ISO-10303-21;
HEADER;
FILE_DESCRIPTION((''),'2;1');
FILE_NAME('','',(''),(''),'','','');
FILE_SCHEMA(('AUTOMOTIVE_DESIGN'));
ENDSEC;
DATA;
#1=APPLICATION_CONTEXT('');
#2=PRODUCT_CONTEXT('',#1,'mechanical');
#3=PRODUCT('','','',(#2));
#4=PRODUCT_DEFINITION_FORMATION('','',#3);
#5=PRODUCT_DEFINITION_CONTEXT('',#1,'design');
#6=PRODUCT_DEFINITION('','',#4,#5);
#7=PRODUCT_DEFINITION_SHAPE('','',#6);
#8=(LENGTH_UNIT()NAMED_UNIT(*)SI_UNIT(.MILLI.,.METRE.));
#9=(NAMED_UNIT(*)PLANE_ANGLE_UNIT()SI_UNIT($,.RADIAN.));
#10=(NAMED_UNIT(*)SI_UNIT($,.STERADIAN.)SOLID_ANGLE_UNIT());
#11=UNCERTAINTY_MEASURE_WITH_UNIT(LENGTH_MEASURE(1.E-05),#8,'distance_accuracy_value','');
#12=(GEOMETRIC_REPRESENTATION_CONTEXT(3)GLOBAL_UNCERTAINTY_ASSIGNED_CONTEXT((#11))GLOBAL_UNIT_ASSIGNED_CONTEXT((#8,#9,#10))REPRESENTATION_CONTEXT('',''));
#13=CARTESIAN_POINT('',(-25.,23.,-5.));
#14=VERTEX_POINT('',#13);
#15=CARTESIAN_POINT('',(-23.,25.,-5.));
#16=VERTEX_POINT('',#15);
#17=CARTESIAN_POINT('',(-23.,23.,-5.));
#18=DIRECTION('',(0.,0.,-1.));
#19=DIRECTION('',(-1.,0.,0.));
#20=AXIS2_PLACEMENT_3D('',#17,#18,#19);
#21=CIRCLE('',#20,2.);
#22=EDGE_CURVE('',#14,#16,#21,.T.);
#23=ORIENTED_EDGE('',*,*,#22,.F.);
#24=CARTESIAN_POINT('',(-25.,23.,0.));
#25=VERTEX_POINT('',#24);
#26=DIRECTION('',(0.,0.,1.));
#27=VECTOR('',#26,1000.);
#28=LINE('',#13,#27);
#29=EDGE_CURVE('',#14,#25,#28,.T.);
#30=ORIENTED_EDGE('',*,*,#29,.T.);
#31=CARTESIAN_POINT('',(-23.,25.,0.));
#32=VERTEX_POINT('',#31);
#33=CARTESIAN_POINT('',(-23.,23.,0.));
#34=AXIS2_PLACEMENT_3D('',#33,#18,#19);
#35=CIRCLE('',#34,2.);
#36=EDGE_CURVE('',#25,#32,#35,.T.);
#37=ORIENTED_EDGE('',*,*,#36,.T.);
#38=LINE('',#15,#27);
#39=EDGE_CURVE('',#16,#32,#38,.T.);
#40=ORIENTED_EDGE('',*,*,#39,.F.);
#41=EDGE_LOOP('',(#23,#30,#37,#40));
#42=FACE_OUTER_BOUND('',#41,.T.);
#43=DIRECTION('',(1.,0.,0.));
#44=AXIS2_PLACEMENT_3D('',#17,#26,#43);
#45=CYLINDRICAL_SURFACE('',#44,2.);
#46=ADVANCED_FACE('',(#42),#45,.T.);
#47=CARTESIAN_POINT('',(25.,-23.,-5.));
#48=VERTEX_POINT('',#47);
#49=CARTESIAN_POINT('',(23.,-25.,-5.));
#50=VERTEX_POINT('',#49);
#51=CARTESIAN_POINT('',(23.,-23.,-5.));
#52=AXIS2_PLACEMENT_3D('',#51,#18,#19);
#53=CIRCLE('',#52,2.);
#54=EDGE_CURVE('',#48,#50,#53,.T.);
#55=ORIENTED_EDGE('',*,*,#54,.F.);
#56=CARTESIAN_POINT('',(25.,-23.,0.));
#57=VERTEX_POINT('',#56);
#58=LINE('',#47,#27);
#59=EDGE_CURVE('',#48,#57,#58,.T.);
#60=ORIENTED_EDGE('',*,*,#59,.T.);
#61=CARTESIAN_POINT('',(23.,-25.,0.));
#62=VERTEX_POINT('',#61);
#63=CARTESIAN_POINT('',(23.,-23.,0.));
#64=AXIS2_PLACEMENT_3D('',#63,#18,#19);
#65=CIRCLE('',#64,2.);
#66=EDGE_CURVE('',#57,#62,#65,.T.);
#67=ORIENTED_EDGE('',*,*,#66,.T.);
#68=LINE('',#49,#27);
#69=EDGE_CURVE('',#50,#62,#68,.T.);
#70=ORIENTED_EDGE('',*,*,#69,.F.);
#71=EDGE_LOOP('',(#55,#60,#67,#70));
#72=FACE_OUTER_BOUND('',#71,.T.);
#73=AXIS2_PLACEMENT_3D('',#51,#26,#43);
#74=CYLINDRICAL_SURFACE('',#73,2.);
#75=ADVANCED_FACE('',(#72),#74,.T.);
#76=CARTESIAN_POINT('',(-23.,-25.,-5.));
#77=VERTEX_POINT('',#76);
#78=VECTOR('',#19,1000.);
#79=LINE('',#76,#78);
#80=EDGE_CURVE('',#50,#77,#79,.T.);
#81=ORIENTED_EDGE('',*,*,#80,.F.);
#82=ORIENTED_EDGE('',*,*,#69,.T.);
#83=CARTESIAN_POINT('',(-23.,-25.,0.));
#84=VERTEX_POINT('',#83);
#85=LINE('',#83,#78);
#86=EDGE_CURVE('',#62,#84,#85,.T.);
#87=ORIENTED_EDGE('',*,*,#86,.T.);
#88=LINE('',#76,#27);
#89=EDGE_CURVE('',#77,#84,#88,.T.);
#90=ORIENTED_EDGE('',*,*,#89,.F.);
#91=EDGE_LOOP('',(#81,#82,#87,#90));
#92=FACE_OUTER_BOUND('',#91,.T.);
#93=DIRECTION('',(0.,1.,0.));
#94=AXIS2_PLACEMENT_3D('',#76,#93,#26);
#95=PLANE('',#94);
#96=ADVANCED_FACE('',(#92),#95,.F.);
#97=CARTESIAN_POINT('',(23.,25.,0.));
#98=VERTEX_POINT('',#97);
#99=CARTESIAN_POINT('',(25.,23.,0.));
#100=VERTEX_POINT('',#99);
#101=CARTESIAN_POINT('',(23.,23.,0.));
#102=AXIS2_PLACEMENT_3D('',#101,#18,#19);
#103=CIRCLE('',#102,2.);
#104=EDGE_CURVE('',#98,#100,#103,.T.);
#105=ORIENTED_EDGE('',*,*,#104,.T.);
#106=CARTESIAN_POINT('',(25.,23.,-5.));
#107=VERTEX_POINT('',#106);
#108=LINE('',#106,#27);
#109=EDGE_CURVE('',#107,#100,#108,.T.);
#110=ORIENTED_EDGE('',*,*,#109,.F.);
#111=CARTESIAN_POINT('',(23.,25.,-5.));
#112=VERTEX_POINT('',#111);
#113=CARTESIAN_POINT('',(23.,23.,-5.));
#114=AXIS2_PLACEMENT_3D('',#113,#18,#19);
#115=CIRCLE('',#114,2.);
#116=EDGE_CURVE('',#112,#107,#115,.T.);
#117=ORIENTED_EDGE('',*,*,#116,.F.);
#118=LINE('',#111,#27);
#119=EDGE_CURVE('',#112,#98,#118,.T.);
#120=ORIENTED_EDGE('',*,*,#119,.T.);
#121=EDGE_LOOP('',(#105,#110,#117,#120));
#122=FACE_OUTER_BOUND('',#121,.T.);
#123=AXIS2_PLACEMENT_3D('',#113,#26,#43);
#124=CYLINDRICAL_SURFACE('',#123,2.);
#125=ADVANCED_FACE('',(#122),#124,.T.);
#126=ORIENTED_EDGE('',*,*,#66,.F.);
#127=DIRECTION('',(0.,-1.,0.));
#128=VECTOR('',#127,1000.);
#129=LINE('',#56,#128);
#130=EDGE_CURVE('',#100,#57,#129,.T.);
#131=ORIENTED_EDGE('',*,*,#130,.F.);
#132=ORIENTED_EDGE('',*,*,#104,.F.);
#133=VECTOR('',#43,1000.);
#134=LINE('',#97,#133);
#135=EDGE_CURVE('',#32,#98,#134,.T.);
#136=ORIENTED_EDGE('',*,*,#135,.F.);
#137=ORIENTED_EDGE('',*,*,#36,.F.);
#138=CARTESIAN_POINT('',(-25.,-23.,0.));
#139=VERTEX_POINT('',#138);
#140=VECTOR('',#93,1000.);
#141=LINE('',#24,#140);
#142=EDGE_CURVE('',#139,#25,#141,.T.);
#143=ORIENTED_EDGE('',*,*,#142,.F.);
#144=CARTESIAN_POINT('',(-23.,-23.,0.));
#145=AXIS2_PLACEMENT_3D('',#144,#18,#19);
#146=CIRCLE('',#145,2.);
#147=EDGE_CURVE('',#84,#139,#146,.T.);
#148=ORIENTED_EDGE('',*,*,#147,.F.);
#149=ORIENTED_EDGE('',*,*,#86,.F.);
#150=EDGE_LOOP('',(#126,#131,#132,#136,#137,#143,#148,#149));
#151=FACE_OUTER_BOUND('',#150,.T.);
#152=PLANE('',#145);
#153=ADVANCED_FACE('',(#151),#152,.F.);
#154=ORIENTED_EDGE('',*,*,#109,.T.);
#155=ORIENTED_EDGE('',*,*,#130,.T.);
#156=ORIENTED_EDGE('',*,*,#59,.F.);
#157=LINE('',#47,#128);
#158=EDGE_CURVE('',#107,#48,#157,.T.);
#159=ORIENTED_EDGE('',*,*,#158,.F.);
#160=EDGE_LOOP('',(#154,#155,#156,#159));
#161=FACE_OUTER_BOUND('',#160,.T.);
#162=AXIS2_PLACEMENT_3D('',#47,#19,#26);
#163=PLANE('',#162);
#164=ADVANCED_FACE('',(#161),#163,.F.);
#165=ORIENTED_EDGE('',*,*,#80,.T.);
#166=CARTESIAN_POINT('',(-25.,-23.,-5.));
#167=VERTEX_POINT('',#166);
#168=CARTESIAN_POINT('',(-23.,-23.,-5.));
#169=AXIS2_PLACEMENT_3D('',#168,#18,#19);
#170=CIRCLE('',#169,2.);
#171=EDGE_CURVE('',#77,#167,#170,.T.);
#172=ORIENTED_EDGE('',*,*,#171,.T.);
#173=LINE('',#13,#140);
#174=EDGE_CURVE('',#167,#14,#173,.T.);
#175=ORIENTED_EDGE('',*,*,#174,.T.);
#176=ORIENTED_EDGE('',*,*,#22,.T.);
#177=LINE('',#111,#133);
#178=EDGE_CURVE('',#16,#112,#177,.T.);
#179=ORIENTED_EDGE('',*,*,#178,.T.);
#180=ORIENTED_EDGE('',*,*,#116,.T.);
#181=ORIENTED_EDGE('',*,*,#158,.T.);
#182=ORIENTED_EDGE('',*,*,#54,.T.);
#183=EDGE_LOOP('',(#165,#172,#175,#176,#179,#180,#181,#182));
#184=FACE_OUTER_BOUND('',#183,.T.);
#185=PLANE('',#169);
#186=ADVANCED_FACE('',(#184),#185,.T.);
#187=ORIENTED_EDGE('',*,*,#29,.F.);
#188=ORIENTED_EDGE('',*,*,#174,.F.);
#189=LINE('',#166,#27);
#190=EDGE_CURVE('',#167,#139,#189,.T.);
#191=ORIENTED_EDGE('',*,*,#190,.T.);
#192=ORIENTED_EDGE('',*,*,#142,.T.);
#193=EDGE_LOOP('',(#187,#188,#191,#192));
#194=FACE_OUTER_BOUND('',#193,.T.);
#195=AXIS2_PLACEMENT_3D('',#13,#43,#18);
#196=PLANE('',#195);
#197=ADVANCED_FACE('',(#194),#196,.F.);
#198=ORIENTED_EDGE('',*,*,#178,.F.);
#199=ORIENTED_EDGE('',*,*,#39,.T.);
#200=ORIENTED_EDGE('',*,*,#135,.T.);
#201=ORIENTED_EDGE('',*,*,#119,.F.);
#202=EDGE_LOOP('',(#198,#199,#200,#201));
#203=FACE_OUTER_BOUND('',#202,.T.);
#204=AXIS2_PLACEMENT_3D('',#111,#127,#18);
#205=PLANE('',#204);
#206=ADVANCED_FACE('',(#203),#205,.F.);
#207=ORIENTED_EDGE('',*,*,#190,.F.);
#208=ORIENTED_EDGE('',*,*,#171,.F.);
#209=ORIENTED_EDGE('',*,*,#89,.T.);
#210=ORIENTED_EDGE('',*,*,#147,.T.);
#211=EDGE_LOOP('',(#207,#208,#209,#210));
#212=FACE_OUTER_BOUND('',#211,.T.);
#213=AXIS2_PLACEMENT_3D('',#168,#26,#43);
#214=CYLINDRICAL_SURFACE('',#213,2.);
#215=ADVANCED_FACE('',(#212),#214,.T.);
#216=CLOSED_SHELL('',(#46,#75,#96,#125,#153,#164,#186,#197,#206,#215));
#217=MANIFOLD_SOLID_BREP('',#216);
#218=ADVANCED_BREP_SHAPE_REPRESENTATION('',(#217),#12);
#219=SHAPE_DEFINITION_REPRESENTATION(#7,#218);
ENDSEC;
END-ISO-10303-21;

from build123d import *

# Parameters (mm, degrees)
SKETCH1_W           = 60
SKETCH1_H           = 60
SKETCH1_W_2         = 52
SKETCH1_H_2         = 52
BOSS_EXTRUDE1_DEPTH = 400
FILLET1_R           = 6
FILLET2_R           = 3
BOSS_EXTRUDE2_DEPTH = 5
CUT_EXTRUDE1_DEPTH  = 403.243707222


with BuildPart() as part:
    # Sketch1 → Boss-Extrude1 (new body)
    with BuildSketch(Plane.XY):
        Rectangle(SKETCH1_W, SKETCH1_H)
        Rectangle(SKETCH1_W_2, SKETCH1_H_2, mode=Mode.SUBTRACT)
    extrude(amount=BOSS_EXTRUDE1_DEPTH)

    # Fillet1
    fillet1_edges = [part.edges().sort_by_distance(p)[0] for p in [
        (30, -30, 200),
        (-30, -30, 200),
        (-30, 30, 200),
        (30, 30, 200),
    ]]
    fillet(fillet1_edges, radius=FILLET1_R)

    # Fillet2
    fillet2_edges = [part.edges().sort_by_distance(p)[0] for p in [
        (26, -26, 200),
        (26, 26, 200),
        (-26, 26, 200),
        (-26, -26, 200),
    ]]
    fillet(fillet2_edges, radius=FILLET2_R)

    # Sketch4 → Cut-Extrude1 (cut, through all)
    with BuildSketch(Plane(origin=(0, 0, 0), x_dir=(-1, 0, 0), z_dir=(0, 0, -1))):
        with BuildLine():
            Line((-30, 24), (-30, -24))
            ThreePointArc((-30, -24), (-28.242640687, -28.242640687), (-24, -30))
            Line((-24, -30), (24, -30))
            ThreePointArc((24, -30), (28.242640687, -28.242640687), (30, -24))
            Line((30, -24), (30, 24))
            ThreePointArc((30, 24), (28.242640687, 28.242640687), (24, 30))
            Line((24, 30), (-24, 30))
            ThreePointArc((-24, 30), (-28.242640687, 28.242640687), (-30, 24))
        make_face()
    extrude(amount=-CUT_EXTRUDE1_DEPTH, mode=Mode.SUBTRACT)


with BuildPart() as body_2:
    # Sketch2 → Boss-Extrude2 (new body)
    with BuildSketch(Plane(origin=(0, 0, 0), x_dir=(-1, 0, 0), z_dir=(0, 0, -1))):
        with BuildLine():
            Line((25, 23), (25, -23))
            ThreePointArc((25, -23), (24.414213562, -24.414213562), (23, -25))
            Line((23, -25), (-23, -25))
            ThreePointArc((-23, -25), (-24.414213562, -24.414213562), (-25, -23))
            Line((-25, -23), (-25, 23))
            ThreePointArc((-25, 23), (-24.414213562, 24.414213562), (-23, 25))
            Line((-23, 25), (23, 25))
            ThreePointArc((23, 25), (24.414213562, 24.414213562), (25, 23))
        make_face()
    extrude(amount=BOSS_EXTRUDE2_DEPTH)


solid = body_2.part
